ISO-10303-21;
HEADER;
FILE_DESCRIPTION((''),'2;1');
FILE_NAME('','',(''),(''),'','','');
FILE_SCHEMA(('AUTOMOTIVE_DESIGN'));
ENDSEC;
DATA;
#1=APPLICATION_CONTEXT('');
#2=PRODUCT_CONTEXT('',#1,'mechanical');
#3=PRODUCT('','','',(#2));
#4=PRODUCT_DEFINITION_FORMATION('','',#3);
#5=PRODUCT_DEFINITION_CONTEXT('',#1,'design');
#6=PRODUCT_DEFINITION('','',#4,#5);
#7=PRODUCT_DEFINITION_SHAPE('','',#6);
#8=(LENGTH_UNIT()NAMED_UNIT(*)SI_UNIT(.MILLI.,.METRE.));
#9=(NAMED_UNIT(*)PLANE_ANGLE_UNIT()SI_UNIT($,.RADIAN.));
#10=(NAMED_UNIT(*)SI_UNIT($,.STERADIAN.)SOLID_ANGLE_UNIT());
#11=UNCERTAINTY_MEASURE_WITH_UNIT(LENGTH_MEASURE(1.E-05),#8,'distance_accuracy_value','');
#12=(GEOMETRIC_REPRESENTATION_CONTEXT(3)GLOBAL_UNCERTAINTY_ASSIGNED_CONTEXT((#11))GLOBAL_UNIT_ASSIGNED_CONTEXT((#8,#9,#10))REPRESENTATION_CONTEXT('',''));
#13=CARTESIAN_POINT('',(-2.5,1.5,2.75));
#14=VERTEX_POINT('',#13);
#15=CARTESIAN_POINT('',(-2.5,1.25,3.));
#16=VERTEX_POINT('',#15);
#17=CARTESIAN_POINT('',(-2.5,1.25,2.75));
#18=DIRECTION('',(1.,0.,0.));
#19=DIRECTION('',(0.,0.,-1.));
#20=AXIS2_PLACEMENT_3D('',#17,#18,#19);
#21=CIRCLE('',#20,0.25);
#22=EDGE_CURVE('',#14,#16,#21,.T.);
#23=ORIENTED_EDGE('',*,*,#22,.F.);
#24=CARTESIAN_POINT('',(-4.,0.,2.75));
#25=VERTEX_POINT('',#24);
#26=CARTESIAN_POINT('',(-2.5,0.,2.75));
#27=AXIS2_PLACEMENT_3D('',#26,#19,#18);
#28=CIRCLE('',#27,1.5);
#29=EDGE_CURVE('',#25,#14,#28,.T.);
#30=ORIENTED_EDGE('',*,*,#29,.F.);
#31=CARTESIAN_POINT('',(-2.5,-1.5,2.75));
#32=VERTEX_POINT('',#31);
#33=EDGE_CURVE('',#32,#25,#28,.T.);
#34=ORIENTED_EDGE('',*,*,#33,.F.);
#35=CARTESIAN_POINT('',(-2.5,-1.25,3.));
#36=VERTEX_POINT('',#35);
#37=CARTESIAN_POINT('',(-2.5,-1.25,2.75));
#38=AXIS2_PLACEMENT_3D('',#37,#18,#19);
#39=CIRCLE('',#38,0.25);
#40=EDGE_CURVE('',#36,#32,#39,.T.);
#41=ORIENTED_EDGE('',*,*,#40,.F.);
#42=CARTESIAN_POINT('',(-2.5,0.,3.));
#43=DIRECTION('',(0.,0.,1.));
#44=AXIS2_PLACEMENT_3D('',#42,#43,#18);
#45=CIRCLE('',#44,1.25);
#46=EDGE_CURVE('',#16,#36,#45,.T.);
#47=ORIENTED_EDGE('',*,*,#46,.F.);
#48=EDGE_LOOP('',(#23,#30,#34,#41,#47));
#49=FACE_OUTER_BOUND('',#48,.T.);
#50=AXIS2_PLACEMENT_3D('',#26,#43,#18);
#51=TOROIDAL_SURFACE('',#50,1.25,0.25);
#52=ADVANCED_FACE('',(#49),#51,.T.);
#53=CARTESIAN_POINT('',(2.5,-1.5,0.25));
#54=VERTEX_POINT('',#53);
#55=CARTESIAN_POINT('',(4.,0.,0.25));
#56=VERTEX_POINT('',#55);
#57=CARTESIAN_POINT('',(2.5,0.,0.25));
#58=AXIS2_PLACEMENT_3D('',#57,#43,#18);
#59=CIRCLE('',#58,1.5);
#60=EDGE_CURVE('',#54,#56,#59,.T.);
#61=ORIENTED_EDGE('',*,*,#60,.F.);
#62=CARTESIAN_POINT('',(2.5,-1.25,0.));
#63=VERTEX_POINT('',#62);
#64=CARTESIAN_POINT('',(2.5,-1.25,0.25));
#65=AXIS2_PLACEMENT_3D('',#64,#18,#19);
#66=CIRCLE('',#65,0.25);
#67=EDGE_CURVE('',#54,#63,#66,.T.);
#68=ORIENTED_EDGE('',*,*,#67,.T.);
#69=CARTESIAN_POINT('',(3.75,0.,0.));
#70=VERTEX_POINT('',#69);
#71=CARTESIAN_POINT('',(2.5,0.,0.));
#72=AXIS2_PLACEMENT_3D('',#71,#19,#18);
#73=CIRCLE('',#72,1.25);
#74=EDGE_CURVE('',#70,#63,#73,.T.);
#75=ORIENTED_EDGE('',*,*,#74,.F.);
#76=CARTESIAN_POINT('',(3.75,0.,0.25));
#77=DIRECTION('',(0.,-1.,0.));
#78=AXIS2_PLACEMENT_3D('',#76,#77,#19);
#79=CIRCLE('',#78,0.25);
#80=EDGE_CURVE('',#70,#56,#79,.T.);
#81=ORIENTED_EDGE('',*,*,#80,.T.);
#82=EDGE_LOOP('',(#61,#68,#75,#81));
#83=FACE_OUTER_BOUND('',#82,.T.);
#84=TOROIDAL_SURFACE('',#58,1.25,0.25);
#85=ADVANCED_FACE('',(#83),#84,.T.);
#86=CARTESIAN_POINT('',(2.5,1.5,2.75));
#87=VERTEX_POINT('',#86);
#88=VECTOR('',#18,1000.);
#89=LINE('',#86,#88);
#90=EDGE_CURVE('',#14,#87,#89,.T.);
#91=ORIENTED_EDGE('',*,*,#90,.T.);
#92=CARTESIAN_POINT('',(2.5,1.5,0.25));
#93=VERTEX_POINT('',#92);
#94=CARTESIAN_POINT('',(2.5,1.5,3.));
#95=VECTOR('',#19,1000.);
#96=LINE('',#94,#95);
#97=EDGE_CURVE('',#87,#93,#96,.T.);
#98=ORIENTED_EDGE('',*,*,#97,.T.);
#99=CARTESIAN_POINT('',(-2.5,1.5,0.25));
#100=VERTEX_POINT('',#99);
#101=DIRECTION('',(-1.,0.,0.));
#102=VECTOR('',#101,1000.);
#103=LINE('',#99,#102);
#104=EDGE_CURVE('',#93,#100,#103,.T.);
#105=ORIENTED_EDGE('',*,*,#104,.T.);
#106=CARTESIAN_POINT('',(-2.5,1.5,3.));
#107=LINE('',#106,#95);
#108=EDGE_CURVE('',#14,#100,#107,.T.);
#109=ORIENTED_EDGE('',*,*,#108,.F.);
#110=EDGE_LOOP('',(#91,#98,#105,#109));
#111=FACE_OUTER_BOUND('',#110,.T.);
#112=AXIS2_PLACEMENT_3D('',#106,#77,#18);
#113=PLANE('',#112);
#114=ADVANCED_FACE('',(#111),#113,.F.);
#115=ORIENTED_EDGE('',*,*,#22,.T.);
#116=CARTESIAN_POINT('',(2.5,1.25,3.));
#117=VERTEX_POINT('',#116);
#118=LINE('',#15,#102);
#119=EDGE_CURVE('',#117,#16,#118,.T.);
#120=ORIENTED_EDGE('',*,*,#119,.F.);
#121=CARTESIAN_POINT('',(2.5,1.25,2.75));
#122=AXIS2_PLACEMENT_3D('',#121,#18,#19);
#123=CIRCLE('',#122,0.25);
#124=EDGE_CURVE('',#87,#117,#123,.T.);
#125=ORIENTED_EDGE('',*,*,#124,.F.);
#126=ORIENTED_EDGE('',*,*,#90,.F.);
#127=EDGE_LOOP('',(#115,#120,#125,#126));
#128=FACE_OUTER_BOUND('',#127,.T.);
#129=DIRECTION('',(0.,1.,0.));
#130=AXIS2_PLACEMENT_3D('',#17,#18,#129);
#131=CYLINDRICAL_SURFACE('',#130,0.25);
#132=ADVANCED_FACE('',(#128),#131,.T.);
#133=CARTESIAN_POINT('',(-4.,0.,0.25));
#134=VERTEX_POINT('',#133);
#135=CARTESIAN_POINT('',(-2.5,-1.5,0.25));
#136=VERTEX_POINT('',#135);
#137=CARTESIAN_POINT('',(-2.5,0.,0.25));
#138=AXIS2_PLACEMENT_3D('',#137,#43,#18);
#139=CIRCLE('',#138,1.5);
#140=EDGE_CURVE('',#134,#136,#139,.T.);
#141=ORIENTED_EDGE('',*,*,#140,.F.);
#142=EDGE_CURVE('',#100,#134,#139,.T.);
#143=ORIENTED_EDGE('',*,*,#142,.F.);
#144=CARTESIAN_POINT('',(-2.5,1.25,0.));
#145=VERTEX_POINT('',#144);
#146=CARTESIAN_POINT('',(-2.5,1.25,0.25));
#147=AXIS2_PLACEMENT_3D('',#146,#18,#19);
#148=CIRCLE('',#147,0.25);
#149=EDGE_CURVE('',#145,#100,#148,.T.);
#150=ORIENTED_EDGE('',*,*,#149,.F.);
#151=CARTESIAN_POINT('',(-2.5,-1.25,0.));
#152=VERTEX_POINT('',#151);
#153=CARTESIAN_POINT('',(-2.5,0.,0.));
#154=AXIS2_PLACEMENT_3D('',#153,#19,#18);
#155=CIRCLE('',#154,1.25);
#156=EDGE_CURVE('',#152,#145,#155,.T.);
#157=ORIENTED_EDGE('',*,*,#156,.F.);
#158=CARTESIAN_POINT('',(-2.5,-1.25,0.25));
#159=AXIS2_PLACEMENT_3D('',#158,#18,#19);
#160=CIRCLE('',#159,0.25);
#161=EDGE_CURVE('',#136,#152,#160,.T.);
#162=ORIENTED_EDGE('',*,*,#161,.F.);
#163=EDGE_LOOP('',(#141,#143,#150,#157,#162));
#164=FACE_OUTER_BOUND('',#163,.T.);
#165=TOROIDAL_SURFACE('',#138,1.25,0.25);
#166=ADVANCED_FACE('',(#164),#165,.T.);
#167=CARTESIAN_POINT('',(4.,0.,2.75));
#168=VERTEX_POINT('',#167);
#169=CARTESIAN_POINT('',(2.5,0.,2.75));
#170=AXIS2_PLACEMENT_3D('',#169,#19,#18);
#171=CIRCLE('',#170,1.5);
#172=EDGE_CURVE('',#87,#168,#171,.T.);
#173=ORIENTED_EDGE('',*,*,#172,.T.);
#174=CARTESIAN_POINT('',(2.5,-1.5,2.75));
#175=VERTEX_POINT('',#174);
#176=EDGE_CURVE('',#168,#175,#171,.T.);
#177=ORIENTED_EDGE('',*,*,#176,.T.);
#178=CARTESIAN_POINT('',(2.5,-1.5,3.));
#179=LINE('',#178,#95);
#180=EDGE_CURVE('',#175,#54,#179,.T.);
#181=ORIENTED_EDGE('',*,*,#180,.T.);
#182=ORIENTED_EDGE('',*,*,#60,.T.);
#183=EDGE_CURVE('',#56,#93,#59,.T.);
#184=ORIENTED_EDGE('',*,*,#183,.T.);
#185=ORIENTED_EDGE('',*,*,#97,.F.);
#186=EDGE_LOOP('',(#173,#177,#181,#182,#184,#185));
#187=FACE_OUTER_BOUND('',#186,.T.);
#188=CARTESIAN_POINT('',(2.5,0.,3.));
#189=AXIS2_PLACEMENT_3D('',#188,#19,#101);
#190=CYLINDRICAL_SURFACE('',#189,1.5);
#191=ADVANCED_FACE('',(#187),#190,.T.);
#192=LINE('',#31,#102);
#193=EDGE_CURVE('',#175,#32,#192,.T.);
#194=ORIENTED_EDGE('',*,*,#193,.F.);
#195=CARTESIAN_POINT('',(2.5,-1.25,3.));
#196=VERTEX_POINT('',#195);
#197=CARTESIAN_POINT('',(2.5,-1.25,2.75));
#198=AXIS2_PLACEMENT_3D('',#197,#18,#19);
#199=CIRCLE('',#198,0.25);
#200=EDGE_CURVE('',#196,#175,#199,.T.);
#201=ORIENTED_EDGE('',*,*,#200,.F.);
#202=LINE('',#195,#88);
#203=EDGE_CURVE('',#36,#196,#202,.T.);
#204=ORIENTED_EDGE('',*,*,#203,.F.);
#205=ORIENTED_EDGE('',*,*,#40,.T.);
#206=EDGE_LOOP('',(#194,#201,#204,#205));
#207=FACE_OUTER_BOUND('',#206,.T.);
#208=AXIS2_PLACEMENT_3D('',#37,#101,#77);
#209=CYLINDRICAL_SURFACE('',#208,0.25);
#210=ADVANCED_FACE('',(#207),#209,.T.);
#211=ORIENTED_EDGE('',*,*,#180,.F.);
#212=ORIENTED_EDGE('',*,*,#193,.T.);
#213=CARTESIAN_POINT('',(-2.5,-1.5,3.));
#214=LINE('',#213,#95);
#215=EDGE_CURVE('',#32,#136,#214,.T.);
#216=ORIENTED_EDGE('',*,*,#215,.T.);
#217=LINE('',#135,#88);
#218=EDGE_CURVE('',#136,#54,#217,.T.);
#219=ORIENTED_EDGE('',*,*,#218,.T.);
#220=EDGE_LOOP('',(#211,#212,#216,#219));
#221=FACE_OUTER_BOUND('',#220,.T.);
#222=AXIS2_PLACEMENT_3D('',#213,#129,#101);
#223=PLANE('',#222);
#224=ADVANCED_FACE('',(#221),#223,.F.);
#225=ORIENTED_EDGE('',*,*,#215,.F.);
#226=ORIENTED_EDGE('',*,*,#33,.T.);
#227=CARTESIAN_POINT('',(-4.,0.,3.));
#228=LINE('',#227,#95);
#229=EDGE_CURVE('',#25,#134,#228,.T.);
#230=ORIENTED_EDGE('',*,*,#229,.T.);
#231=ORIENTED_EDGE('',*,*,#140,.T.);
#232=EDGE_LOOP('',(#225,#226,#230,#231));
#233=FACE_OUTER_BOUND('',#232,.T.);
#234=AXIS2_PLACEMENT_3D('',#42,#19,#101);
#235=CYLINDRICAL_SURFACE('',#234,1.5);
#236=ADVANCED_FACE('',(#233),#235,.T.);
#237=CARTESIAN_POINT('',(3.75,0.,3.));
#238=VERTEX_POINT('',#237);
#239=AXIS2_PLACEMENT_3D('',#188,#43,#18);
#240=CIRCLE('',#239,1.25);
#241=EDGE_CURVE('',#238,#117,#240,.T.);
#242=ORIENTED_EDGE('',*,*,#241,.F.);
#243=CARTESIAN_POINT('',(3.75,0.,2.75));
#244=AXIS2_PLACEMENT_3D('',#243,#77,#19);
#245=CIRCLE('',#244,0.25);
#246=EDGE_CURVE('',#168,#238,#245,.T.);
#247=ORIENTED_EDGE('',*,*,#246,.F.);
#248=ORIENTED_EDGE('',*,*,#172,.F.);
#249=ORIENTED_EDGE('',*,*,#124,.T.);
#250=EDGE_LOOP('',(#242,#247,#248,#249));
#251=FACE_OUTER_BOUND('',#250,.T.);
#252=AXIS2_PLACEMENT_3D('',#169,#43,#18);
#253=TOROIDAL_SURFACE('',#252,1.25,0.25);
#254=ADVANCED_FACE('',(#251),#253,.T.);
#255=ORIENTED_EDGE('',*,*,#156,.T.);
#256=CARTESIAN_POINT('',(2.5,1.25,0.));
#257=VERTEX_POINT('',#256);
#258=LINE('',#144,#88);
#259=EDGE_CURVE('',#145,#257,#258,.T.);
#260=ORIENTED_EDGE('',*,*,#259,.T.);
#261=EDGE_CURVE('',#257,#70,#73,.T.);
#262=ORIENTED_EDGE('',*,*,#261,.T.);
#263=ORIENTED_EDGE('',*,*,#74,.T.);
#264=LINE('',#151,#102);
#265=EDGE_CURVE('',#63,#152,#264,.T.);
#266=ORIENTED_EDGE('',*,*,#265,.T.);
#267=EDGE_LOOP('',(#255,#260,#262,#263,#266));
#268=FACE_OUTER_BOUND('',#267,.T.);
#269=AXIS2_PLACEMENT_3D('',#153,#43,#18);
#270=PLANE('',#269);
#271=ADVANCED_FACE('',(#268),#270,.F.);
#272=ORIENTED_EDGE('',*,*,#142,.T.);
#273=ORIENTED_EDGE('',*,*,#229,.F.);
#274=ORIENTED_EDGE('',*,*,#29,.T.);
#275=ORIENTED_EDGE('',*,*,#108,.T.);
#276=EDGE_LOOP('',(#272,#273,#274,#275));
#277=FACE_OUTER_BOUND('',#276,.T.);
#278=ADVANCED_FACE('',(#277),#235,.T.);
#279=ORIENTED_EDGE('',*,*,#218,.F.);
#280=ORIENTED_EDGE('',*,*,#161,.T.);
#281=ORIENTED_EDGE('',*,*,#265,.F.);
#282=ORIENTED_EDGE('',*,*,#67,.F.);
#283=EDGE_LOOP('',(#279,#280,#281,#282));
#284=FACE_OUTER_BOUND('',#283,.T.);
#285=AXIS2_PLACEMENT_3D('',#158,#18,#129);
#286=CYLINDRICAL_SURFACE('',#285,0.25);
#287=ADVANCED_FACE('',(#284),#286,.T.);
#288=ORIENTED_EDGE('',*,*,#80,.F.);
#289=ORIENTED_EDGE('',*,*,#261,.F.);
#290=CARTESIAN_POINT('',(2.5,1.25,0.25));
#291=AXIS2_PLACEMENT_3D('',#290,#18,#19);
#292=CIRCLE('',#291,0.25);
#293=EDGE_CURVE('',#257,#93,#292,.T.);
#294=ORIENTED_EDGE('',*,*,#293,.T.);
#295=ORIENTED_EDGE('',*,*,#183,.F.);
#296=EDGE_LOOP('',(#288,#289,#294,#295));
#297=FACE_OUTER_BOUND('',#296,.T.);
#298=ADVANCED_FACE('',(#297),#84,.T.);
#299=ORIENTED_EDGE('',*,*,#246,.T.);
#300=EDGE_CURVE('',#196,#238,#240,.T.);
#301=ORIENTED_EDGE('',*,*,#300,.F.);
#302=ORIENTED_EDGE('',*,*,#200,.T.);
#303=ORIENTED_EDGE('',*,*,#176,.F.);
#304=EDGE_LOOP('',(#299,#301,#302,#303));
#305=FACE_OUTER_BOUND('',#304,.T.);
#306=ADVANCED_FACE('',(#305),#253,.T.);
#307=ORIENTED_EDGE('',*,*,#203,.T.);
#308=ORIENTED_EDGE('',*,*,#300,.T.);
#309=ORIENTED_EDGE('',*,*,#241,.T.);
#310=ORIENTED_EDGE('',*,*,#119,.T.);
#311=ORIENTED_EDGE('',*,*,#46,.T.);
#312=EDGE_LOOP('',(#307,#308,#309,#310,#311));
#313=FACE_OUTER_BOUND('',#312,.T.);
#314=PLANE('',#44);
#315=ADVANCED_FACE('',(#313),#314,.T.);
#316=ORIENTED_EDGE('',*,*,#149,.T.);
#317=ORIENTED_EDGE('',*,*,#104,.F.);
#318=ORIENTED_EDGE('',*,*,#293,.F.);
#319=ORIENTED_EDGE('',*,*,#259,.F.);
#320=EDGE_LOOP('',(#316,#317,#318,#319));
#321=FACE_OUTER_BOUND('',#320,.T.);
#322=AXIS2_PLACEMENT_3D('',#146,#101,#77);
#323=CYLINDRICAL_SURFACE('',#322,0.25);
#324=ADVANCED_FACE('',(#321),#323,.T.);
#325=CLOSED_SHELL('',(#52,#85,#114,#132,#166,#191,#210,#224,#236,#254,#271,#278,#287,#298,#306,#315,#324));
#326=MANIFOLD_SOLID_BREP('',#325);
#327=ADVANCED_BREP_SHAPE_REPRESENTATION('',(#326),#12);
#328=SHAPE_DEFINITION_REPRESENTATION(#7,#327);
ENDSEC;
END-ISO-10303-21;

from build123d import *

# Parameters (mm, degrees)
BASE_EXTRUDE_DEPTH = 3
FILLET1_R          = 0.25


with BuildPart() as part:
    # Sketch1 → Base-Extrude (new body)
    with BuildSketch(Plane.XY):
        with BuildLine():
            Line((-2.5, 1.5), (2.5, 1.5))
            ThreePointArc((2.5, 1.5), (4, 0), (2.5, -1.5))
            Line((2.5, -1.5), (-2.5, -1.5))
            ThreePointArc((-2.5, -1.5), (-4, 0), (-2.5, 1.5))
        make_face()
    extrude(amount=BASE_EXTRUDE_DEPTH)

    # Fillet1
    fillet1_edges = [part.edges().sort_by_distance(p)[0] for p in [
        (4, 0, 3),
        (0, 1.5, 3),
        (-4, 0, 3),
        (0, 1.5, 0),
        (4, 0, 0),
        (0, -1.5, 0),
        (-4, 0, 0),
        (0, -1.5, 3),
    ]]
    fillet(fillet1_edges, radius=FILLET1_R)


solid = part.part
